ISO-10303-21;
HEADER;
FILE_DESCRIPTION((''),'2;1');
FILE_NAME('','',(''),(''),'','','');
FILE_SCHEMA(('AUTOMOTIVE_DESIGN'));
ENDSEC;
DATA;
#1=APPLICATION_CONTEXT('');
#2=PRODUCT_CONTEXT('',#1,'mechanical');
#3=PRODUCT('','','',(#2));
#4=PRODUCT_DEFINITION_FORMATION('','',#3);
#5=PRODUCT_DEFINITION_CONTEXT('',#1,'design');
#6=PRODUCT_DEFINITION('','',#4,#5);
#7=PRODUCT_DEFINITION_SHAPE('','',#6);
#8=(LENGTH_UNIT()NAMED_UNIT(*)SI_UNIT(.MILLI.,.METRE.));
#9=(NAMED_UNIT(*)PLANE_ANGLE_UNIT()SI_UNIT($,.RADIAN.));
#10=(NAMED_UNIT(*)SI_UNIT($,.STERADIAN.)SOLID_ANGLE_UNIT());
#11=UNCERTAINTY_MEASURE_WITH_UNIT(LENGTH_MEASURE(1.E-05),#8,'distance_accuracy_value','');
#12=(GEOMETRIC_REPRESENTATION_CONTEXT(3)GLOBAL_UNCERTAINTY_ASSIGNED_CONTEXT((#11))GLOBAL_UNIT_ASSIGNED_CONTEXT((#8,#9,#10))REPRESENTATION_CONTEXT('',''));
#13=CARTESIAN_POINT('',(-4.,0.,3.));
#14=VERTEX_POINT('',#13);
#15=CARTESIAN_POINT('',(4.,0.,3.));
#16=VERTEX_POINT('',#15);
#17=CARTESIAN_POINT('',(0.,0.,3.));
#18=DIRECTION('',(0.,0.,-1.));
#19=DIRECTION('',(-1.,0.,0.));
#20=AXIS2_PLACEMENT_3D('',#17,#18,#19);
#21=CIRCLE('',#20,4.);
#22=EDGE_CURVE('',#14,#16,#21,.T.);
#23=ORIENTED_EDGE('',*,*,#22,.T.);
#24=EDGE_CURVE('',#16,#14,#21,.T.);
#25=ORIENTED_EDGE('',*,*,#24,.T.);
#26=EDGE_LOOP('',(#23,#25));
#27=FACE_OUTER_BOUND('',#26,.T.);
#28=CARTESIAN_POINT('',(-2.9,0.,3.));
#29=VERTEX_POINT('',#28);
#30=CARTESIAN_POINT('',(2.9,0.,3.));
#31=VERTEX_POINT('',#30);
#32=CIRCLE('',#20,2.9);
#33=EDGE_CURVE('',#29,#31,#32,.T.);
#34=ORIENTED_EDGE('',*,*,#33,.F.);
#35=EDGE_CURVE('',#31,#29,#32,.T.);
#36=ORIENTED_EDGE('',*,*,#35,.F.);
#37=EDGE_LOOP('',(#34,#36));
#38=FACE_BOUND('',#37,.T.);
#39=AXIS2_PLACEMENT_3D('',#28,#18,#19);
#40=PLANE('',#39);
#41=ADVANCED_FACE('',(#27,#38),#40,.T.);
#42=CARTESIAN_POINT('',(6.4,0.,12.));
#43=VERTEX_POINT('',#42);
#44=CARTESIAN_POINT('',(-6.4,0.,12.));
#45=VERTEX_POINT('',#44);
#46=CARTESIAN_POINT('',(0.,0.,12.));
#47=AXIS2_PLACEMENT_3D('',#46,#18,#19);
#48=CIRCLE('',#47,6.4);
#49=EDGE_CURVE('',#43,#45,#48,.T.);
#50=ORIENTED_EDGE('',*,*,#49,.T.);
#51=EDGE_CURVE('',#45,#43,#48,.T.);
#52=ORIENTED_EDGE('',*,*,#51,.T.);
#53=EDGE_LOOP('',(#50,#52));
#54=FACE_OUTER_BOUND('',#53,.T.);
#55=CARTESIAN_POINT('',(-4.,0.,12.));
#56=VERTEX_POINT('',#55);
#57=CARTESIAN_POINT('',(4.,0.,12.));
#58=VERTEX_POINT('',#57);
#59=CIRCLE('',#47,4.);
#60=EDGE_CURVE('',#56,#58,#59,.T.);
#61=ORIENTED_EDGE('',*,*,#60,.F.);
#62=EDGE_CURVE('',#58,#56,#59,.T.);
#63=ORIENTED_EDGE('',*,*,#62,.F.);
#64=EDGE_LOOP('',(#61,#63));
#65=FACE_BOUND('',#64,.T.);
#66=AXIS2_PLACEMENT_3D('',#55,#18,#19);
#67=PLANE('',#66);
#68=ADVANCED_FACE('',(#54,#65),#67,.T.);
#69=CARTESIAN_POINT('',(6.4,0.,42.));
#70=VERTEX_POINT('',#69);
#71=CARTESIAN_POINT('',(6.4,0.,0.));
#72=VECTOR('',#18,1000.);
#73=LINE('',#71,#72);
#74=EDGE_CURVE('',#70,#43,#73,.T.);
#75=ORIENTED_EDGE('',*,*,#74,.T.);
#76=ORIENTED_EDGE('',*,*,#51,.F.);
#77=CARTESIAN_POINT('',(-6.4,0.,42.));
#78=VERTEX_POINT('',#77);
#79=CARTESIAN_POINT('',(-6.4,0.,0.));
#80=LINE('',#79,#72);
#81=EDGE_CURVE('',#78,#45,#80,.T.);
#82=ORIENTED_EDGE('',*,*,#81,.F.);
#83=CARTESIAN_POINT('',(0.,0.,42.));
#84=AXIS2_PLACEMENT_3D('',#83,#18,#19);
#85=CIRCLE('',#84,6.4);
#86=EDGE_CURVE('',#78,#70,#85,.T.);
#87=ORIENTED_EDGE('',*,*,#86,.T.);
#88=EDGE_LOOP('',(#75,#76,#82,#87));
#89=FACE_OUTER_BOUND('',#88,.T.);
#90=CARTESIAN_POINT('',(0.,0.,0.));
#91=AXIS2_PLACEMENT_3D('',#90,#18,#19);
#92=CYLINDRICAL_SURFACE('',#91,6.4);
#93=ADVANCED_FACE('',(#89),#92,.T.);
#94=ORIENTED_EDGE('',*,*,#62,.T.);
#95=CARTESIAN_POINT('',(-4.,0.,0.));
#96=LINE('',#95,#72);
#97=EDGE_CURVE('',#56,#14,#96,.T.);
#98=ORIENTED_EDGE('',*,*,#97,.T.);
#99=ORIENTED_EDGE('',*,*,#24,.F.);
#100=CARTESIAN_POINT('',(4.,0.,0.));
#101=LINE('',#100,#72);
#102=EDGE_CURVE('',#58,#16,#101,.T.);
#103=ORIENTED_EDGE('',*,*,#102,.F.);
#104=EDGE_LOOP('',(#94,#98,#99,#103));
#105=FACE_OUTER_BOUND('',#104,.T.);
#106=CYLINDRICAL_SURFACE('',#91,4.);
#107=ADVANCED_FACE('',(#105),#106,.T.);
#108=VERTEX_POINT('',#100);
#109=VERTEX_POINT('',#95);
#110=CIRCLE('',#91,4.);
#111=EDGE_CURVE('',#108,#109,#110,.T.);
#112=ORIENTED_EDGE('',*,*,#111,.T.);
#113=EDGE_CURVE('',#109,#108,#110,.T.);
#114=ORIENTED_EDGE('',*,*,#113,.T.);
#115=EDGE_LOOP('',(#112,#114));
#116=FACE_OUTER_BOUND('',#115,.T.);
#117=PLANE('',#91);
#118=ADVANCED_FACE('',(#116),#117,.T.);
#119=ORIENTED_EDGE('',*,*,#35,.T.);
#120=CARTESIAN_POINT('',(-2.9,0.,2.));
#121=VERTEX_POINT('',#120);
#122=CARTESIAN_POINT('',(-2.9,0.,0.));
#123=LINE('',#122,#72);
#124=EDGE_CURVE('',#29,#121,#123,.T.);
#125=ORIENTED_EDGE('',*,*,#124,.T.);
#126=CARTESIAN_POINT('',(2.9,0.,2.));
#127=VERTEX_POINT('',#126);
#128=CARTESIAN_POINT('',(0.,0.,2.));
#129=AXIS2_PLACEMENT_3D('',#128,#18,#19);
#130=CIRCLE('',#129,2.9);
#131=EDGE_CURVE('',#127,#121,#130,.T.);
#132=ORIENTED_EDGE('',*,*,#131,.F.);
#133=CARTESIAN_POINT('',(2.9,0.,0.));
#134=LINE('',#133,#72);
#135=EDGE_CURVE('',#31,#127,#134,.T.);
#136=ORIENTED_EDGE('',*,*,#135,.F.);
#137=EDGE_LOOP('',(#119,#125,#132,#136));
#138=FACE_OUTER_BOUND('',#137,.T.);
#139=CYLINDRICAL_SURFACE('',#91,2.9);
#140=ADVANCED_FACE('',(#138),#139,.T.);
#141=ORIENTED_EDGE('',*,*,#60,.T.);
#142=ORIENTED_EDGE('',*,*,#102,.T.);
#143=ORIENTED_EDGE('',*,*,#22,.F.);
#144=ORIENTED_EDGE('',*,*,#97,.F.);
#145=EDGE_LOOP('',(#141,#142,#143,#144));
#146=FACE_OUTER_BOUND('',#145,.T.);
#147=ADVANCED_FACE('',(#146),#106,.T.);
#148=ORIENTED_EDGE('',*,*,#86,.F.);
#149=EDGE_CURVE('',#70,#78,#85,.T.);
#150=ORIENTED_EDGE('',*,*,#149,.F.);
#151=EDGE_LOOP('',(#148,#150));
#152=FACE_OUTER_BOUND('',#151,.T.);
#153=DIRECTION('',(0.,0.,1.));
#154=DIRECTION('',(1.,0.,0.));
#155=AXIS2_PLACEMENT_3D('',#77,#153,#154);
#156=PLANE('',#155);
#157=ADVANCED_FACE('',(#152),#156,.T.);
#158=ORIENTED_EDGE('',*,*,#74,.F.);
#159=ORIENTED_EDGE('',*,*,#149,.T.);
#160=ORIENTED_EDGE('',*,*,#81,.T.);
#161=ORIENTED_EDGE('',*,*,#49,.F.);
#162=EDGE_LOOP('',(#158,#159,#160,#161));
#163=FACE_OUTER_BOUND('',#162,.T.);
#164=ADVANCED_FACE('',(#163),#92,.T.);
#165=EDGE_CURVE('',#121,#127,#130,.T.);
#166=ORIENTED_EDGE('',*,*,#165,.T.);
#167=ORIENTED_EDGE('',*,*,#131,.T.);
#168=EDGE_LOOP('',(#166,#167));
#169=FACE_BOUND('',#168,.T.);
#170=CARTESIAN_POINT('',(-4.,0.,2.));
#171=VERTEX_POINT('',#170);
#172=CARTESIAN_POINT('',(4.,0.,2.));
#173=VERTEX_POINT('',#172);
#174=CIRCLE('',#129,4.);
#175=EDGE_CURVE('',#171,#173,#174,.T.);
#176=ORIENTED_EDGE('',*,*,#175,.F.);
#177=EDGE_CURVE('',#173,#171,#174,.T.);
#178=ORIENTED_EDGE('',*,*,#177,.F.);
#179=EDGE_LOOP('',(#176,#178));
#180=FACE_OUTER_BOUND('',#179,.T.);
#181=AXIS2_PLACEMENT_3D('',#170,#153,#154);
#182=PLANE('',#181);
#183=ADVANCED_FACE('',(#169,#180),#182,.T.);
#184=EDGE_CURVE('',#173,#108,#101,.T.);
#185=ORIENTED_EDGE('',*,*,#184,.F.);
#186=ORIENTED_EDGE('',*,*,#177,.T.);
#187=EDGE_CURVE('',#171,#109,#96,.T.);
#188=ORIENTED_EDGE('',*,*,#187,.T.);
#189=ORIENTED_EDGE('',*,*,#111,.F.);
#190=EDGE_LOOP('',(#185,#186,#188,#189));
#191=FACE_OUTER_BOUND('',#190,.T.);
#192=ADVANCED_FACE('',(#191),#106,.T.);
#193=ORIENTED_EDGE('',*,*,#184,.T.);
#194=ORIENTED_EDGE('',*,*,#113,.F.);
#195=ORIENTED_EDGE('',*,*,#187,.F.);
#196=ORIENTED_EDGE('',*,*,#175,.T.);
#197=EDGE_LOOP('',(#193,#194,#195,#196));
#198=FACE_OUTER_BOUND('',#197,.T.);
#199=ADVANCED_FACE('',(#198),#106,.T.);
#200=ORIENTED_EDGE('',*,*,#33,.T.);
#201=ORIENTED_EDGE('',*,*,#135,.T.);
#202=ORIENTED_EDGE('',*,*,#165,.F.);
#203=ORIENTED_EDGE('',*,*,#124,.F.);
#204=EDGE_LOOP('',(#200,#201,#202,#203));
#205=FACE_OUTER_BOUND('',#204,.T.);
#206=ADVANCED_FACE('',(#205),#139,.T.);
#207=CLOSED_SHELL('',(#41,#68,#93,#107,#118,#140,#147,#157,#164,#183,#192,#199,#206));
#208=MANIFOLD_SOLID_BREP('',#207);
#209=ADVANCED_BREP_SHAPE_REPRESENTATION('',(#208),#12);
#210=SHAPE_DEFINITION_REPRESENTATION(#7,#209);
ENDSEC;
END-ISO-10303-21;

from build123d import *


with BuildPart() as part:
    # 草图1 → 旋转1 (revolve)
    with BuildSketch(Plane(origin=(0, 0, 0), x_dir=(1, 0, 0), z_dir=(0, 1, 0))):
        Polygon((0, 0), (-4, 0), (-4, -2), (-2.9, -2), (-2.9, -3), (-4, -3), (-4, -12), (-6.4, -12), (-6.4, -42), (0, -42), align=None)
    revolve(axis=Axis((0, 0, 0), (0, 0, 1)))


solid = part.part
